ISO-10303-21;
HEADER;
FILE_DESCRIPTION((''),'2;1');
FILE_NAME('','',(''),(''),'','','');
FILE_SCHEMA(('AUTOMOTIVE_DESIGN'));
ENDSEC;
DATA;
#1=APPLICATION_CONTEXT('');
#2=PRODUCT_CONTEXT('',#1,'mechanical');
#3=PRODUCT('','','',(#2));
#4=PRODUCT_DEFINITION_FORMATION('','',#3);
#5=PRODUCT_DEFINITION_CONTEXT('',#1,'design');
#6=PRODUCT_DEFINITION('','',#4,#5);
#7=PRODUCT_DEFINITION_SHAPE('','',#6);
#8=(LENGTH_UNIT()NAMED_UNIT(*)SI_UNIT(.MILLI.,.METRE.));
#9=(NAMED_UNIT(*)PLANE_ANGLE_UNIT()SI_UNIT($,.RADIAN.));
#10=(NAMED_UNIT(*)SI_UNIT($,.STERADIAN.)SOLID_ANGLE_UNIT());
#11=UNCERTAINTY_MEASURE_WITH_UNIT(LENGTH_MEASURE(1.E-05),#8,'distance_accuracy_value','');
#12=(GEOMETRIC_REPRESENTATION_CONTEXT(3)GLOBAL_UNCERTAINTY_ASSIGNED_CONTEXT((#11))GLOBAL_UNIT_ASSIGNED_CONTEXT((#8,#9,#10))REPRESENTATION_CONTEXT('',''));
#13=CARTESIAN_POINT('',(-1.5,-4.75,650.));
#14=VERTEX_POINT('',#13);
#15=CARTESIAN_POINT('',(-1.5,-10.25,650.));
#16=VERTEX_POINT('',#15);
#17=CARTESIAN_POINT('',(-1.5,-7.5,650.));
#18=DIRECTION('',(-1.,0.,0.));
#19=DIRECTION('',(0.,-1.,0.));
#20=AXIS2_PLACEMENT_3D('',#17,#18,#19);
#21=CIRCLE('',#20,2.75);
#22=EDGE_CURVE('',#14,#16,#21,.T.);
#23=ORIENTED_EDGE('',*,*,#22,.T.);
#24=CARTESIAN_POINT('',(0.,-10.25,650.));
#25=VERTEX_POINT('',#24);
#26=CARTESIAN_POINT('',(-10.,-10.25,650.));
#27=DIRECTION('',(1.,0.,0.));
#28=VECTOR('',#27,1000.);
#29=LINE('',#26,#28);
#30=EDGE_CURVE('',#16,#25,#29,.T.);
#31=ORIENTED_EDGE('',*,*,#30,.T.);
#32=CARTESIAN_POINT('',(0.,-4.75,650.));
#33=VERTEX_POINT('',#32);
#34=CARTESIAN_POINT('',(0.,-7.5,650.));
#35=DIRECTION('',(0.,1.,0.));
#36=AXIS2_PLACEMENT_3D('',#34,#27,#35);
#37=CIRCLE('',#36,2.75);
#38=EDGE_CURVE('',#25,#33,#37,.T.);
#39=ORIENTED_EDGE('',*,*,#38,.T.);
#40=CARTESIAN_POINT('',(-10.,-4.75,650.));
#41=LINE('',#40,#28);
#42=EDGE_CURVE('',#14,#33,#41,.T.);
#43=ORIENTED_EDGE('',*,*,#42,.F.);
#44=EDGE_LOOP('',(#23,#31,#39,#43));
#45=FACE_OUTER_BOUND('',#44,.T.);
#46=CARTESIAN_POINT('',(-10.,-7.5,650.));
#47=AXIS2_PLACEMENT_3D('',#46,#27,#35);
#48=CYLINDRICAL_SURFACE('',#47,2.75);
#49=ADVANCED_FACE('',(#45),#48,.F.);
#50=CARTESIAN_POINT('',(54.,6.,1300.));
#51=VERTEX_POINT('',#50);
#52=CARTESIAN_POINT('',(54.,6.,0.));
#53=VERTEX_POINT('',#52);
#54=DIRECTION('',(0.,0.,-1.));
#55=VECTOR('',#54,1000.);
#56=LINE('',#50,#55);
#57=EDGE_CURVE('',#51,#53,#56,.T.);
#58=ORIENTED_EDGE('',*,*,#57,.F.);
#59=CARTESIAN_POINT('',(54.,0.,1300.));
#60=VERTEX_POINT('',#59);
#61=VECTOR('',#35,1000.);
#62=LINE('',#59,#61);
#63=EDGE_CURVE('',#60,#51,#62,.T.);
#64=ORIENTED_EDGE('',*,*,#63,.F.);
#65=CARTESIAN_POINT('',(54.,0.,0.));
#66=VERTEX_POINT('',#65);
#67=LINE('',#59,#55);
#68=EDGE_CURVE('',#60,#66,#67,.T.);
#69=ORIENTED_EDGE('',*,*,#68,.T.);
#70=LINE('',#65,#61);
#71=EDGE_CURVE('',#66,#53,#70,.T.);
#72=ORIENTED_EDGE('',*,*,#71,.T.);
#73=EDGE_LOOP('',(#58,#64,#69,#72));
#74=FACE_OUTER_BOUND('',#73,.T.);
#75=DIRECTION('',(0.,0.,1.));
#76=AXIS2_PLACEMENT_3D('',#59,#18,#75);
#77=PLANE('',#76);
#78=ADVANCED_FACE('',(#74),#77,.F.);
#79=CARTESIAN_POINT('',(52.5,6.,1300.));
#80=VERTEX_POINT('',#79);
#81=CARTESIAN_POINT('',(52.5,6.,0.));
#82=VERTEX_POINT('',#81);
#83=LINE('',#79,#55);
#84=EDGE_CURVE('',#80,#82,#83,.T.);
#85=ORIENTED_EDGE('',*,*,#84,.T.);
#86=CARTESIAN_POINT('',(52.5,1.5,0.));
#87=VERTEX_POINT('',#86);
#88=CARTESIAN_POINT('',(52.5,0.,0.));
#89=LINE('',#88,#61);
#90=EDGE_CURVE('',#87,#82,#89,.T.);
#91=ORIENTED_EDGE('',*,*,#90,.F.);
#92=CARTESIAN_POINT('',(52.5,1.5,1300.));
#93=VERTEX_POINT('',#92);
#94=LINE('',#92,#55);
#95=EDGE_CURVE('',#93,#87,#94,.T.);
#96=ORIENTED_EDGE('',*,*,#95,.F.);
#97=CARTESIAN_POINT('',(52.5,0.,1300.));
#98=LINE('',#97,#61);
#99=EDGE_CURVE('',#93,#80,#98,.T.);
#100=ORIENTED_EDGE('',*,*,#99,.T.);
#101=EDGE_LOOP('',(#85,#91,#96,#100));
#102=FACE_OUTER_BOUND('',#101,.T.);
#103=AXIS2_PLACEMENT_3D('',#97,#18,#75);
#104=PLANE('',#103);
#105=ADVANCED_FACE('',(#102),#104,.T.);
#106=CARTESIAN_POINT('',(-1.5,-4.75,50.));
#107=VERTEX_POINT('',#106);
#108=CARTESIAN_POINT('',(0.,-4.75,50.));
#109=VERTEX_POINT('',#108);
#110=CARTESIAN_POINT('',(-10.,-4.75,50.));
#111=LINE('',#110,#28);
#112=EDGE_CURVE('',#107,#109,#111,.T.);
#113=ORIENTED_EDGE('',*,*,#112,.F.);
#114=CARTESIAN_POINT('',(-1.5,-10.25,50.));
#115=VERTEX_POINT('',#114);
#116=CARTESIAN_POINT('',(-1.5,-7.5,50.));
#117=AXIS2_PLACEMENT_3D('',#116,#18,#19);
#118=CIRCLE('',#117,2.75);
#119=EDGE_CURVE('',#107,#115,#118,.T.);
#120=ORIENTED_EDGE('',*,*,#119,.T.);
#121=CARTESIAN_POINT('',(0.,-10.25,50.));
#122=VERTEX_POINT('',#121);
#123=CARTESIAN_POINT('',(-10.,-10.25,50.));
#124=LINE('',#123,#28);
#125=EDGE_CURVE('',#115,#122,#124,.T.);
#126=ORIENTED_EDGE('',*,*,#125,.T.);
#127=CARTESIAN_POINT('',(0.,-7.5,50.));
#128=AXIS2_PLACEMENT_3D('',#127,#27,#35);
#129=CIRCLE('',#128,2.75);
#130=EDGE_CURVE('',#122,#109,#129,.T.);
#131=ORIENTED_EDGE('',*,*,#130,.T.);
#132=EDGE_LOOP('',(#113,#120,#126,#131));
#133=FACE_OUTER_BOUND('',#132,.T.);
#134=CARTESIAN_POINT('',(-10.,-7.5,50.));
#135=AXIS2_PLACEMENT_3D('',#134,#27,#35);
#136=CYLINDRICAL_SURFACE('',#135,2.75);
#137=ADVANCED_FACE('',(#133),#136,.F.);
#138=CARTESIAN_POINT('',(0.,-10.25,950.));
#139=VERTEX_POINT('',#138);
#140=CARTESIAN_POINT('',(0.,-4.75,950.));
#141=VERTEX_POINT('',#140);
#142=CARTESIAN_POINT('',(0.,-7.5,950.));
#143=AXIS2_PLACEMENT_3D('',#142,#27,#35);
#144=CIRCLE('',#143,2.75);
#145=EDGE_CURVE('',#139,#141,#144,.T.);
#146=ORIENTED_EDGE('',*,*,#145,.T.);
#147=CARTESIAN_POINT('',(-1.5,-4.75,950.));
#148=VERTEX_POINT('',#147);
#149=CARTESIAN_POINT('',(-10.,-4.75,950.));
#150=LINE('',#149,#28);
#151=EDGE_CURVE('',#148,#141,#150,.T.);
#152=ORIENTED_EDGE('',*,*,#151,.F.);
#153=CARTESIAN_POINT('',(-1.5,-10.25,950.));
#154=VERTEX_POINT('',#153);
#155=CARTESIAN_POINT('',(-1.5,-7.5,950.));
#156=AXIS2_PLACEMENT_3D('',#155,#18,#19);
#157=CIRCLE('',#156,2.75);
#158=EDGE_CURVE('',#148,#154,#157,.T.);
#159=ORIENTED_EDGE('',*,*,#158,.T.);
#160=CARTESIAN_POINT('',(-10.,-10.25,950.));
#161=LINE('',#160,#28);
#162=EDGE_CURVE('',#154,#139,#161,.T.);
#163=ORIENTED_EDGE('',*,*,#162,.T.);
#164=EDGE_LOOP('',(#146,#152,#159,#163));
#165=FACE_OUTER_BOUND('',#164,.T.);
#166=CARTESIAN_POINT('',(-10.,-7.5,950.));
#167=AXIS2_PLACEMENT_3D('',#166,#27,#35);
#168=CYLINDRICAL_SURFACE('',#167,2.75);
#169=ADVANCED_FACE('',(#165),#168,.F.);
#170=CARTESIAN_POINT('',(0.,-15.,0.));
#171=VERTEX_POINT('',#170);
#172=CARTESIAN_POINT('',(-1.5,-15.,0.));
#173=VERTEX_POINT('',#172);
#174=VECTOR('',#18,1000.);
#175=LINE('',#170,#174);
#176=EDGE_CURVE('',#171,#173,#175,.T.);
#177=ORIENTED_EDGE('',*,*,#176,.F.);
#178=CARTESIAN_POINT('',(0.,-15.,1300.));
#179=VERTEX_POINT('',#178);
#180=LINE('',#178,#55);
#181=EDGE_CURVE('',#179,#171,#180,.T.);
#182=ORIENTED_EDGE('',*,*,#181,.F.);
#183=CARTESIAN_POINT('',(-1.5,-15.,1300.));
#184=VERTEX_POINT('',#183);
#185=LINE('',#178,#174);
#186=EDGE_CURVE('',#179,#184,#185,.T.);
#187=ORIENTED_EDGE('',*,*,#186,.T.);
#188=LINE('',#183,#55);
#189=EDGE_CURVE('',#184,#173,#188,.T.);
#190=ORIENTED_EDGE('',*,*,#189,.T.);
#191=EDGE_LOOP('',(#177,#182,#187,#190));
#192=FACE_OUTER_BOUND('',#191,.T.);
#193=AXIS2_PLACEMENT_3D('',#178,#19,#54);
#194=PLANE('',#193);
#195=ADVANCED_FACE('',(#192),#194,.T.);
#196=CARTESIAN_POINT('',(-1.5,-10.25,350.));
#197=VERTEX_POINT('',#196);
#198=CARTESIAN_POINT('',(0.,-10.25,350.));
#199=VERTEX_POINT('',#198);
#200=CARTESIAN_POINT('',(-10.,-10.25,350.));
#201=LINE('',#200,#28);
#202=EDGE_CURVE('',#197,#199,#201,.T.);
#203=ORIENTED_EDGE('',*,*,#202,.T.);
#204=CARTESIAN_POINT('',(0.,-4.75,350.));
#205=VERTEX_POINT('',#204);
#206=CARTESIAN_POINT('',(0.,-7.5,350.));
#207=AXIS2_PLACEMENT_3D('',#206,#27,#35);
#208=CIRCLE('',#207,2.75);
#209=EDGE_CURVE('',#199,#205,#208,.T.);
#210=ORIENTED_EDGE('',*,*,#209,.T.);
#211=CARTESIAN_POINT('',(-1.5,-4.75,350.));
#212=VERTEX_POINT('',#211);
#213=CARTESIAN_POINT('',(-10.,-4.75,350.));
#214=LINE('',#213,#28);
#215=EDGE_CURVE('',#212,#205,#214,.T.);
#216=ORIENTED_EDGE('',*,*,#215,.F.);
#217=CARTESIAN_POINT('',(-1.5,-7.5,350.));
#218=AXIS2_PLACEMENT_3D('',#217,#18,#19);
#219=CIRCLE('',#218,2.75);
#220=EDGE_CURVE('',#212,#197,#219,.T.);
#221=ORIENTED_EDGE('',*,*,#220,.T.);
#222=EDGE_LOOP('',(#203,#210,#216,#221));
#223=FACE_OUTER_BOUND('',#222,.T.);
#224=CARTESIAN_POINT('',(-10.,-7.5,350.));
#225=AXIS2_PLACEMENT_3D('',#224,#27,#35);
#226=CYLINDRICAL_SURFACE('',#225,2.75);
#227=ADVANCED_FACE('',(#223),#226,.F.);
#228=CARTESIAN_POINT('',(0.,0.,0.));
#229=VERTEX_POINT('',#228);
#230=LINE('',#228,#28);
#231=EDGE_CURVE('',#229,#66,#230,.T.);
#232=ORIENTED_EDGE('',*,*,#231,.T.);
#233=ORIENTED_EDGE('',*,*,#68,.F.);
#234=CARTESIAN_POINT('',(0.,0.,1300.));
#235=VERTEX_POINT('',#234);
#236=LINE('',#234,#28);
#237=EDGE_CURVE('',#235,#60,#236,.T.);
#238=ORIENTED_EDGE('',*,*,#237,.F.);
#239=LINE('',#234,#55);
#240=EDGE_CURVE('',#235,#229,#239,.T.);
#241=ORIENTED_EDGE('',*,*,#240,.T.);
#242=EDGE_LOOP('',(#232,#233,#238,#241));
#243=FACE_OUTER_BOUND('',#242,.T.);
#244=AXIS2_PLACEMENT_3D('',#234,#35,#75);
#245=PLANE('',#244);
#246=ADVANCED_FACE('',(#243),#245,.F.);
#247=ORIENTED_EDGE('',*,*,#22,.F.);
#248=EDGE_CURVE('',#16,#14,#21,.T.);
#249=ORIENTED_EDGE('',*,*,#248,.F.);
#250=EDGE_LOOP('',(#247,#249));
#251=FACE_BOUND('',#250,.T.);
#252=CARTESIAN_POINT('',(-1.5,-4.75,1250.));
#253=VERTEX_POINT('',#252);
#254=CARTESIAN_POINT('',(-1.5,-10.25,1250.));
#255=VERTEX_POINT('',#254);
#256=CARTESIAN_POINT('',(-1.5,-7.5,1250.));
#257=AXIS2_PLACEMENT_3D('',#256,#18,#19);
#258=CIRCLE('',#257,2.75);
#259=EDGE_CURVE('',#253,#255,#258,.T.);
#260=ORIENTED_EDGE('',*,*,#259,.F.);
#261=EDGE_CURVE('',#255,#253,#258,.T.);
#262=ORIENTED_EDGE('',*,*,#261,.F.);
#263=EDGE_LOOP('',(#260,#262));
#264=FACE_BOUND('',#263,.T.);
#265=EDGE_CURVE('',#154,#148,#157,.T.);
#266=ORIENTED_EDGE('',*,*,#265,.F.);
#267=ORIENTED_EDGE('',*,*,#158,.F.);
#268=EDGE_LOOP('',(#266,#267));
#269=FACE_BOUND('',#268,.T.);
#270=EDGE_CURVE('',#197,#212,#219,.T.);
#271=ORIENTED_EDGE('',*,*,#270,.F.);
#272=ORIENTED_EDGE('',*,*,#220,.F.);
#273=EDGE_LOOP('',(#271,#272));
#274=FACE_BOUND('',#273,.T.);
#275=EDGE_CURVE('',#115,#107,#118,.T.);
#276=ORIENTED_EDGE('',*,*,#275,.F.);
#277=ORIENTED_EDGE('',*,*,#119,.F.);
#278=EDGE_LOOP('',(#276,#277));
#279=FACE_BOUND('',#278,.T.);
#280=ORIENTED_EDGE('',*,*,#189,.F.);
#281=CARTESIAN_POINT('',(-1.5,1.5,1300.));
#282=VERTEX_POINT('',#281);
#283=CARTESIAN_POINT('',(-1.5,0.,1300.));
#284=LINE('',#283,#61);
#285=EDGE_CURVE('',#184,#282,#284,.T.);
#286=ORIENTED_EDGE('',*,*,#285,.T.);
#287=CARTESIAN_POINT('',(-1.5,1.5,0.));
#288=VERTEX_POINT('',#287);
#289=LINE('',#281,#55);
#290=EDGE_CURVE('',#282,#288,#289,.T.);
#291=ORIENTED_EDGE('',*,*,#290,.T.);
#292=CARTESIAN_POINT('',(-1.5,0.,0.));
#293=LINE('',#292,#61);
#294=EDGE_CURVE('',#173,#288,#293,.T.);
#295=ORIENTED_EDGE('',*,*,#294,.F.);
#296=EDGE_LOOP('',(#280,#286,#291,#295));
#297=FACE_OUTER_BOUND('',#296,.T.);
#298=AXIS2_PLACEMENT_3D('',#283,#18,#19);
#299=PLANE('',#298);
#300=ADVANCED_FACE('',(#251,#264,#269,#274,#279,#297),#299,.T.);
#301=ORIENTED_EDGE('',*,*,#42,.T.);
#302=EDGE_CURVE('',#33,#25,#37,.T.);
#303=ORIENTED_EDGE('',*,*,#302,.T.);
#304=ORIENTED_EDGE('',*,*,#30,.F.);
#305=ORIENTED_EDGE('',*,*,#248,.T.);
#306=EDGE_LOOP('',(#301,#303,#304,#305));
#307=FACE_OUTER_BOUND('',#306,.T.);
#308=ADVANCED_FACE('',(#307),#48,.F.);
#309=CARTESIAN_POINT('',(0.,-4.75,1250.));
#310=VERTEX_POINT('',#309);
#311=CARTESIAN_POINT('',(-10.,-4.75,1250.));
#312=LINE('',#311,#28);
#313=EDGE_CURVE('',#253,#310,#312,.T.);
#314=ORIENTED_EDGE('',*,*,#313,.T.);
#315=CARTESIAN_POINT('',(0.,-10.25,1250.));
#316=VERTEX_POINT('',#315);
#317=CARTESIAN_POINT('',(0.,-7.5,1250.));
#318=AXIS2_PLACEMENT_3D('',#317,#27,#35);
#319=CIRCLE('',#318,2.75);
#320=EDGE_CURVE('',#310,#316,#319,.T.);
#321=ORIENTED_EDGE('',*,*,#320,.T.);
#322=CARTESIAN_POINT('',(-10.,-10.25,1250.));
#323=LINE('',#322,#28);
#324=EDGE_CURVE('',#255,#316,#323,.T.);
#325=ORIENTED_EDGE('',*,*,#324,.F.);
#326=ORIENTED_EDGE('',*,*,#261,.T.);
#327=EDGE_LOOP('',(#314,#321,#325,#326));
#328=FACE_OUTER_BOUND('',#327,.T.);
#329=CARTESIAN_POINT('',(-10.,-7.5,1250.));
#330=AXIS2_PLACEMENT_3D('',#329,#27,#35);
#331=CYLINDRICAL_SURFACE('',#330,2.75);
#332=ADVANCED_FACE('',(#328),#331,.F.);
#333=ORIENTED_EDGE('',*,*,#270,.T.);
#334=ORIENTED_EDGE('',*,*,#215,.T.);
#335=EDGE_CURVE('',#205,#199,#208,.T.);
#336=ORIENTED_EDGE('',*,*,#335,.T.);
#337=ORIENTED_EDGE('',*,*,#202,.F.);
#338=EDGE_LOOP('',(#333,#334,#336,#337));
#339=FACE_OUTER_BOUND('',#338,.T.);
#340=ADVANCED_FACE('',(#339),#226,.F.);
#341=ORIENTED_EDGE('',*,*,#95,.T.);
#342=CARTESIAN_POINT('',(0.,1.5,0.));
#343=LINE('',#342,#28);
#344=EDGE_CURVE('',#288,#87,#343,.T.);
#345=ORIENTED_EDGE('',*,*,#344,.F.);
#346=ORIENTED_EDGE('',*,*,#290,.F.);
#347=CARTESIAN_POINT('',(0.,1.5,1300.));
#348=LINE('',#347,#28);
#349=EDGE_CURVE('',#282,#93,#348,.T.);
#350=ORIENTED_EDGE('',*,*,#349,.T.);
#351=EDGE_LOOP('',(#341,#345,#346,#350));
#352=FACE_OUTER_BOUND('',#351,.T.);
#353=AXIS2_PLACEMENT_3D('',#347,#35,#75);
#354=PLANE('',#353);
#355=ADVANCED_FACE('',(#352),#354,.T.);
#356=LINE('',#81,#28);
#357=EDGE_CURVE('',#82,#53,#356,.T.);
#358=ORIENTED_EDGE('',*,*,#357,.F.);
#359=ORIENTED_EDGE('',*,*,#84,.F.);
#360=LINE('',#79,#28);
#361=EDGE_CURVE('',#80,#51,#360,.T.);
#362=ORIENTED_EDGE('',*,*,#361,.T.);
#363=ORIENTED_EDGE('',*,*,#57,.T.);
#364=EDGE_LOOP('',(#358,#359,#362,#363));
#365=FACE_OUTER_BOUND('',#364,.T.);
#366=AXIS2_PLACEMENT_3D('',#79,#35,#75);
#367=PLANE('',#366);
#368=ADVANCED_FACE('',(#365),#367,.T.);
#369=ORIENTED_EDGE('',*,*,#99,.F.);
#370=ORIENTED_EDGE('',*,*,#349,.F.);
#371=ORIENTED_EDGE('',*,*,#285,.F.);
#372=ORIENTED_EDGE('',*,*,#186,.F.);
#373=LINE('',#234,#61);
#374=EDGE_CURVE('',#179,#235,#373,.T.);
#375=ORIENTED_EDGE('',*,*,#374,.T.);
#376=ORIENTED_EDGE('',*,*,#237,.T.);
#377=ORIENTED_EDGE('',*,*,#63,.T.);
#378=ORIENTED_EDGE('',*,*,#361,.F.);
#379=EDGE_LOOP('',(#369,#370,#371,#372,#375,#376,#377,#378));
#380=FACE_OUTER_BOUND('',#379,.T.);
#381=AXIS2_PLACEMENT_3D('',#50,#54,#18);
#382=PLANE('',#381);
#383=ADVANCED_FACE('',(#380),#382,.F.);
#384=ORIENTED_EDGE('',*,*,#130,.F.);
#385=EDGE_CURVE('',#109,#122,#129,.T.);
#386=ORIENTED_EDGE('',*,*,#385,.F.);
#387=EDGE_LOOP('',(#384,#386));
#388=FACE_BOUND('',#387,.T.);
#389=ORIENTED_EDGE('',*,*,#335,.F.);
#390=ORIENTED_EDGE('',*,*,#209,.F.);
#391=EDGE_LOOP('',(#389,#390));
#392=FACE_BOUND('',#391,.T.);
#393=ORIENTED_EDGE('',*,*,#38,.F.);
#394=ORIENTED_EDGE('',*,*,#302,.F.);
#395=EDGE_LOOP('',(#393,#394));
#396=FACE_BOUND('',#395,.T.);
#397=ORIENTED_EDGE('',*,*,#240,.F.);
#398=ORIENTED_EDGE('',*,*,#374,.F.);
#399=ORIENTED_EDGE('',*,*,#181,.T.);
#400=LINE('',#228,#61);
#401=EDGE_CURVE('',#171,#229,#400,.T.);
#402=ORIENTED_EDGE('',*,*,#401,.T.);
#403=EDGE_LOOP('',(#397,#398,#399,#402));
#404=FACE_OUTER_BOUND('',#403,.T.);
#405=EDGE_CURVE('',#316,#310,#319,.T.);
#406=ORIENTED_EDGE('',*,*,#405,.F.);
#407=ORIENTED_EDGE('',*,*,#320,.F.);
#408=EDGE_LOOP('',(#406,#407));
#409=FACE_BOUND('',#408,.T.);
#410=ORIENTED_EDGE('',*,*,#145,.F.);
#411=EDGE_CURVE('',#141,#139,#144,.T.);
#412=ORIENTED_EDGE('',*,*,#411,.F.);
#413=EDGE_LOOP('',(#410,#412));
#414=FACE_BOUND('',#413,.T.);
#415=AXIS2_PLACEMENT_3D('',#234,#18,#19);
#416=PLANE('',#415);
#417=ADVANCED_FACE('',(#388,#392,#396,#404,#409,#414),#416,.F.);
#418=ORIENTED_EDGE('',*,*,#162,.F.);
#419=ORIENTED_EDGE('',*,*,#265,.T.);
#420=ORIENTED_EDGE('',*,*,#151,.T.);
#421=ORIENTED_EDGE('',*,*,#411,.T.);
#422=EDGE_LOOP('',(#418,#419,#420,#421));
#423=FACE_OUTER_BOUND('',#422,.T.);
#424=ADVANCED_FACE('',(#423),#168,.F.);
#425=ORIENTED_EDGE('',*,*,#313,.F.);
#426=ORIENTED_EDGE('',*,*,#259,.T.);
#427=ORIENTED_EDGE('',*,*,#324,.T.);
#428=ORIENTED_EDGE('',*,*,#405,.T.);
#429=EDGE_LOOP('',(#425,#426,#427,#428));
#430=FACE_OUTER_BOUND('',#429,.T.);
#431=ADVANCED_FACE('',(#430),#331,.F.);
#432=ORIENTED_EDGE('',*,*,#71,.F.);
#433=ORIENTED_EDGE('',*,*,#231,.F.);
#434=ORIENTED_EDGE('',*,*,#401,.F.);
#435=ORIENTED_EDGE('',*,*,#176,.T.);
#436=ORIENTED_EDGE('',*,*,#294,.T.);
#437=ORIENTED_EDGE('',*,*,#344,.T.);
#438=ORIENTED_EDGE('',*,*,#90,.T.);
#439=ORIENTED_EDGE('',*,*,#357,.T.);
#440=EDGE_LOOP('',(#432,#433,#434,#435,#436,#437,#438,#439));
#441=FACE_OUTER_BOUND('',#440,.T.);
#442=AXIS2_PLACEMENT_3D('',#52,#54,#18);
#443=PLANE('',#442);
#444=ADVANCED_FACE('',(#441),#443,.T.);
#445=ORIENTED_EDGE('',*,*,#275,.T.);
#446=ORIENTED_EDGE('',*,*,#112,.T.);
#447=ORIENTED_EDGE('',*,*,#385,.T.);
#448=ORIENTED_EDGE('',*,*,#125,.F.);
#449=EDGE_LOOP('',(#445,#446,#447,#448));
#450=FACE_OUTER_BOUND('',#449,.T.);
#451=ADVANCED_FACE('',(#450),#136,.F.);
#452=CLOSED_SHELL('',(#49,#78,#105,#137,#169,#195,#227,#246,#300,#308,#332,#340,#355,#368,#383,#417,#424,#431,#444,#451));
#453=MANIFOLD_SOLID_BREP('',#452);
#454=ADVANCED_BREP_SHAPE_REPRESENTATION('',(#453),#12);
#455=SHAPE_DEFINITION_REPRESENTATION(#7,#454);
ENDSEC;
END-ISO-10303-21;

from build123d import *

# Parameters (mm, degrees)
EXTRUDE_1_DEPTH     = 1300
SKETCH_2_R          = 2.75
CUT_EXTRUDE_1_DEPTH = 10


with BuildPart() as part:
    # 草图1 → 拉伸-薄壁1 (new body)
    with BuildSketch(Plane.XY):
        Polygon((54, 6), (54, 0), (0, 0), (0, -15), (-1.5, -15), (-1.5, 1.5), (52.5, 1.5), (52.5, 6), align=None)
    extrude(amount=EXTRUDE_1_DEPTH)

    # 草图2 → 切除-拉伸1 (cut)
    with BuildSketch(Plane(origin=(0, 0, 0), x_dir=(0, 0, -1), z_dir=(1, 0, 0))):
        with Locations(Location((-1250, -7.5, 0), (0, 0, 90))):
            Circle(SKETCH_2_R)
        with Locations(Location((-950, -7.5, 0), (0, 0, 90))):
            Circle(SKETCH_2_R)
        with Locations(Location((-650, -7.5, 0), (0, 0, 90))):
            Circle(SKETCH_2_R)
        with Locations(Location((-350, -7.5, 0), (0, 0, 90))):
            Circle(SKETCH_2_R)
        with Locations(Location((-50, -7.5, 0), (0, 0, 90))):
            Circle(SKETCH_2_R)
    extrude(amount=-CUT_EXTRUDE_1_DEPTH, mode=Mode.SUBTRACT)


solid = part.part
